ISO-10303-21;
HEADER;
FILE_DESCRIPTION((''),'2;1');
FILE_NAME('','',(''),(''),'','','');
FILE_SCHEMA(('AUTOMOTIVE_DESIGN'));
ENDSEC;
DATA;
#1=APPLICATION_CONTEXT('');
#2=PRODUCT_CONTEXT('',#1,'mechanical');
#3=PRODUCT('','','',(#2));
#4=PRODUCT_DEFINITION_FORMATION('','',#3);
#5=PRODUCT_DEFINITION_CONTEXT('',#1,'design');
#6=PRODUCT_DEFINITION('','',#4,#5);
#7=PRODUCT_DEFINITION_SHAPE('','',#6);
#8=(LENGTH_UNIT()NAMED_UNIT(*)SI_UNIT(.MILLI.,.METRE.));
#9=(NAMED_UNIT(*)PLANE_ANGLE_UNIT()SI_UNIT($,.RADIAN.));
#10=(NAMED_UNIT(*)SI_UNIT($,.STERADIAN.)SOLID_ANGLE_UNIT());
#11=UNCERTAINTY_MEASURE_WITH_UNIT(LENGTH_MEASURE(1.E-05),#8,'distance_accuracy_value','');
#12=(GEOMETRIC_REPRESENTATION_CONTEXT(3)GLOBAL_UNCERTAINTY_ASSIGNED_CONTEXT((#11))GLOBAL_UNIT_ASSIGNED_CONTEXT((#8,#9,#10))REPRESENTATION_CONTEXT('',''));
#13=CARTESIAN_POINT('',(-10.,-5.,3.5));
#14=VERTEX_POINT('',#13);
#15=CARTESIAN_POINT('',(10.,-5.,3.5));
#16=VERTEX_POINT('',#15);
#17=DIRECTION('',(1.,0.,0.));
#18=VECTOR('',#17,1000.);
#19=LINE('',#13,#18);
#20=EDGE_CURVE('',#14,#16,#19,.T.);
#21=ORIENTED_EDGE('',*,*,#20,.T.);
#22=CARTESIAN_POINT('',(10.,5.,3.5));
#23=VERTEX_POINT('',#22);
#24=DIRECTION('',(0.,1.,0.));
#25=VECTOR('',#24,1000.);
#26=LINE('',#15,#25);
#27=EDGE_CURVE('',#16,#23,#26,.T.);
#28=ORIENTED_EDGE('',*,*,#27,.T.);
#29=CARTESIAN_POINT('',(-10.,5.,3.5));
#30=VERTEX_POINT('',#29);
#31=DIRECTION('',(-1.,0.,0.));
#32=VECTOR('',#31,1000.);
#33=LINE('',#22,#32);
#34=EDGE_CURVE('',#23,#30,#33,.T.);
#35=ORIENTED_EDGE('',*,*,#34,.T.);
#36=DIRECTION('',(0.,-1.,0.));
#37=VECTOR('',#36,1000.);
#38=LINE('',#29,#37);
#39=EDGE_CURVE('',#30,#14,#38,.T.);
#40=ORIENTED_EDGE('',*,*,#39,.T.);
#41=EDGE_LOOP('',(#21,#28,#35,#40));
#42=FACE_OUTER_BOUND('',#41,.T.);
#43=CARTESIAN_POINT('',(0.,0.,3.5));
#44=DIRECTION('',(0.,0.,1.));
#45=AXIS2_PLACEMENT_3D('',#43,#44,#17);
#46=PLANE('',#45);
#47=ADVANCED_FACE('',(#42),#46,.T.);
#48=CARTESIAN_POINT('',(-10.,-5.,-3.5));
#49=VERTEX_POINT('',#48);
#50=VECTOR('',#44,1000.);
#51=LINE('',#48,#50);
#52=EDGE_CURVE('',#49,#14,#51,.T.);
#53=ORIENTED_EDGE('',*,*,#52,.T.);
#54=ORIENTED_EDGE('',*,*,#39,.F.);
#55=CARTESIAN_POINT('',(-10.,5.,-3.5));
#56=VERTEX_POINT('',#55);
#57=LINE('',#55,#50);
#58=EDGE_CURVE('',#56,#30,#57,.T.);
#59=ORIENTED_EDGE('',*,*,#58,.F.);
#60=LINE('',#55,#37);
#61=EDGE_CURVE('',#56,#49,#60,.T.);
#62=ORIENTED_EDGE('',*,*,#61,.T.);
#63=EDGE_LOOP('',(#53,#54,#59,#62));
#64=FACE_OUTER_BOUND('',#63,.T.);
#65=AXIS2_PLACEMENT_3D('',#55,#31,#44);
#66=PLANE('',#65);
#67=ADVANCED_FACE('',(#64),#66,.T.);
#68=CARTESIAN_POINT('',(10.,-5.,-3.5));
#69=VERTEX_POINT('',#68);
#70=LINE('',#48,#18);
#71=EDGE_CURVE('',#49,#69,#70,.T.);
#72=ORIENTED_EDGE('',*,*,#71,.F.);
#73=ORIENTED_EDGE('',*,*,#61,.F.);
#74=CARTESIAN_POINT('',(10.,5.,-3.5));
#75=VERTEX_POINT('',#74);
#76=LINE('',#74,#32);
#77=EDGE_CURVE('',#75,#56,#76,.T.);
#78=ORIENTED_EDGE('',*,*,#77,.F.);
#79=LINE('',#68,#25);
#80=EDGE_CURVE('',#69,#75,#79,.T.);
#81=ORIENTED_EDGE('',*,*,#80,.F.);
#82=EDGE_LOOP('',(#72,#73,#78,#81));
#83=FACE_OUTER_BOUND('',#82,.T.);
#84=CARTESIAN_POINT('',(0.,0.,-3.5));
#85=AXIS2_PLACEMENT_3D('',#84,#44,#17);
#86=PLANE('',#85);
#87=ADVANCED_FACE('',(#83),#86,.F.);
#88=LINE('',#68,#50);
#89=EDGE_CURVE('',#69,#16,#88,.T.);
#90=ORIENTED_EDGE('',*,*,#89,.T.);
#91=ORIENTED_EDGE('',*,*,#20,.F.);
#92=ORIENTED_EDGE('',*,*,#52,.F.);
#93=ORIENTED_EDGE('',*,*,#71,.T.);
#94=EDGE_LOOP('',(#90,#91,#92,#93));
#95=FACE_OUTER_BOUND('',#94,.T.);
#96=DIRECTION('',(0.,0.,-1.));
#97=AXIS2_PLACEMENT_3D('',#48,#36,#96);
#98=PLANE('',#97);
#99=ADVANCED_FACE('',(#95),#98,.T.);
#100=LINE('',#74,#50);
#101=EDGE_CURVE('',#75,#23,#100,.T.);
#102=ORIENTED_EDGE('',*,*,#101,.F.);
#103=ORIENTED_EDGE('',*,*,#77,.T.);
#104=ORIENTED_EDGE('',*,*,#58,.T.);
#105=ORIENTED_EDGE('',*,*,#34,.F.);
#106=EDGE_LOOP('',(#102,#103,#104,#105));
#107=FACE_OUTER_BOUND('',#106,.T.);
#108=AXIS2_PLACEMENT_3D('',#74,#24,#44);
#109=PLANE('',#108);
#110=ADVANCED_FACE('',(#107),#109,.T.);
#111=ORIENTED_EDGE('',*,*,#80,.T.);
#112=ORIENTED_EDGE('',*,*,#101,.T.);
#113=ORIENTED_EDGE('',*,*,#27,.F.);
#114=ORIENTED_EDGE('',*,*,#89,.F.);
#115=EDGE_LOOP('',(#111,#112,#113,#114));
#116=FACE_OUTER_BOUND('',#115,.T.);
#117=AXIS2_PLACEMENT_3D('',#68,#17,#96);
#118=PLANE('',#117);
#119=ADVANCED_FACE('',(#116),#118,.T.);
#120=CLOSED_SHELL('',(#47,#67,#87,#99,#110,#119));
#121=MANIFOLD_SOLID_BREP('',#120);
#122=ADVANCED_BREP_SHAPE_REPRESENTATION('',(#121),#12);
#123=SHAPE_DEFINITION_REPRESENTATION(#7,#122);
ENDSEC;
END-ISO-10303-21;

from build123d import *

# Parameters (mm, degrees)
SKETCH_1_W      = 20
SKETCH_1_H      = 10
EXTRUDE_1_DEPTH = 3.5


with BuildPart() as part:
    # 草图1 → 凸台-拉伸1 (new, symmetric)
    with BuildSketch(Plane.XY):
        Rectangle(SKETCH_1_W, SKETCH_1_H)
    extrude(amount=EXTRUDE_1_DEPTH, both=True)


solid = part.part
